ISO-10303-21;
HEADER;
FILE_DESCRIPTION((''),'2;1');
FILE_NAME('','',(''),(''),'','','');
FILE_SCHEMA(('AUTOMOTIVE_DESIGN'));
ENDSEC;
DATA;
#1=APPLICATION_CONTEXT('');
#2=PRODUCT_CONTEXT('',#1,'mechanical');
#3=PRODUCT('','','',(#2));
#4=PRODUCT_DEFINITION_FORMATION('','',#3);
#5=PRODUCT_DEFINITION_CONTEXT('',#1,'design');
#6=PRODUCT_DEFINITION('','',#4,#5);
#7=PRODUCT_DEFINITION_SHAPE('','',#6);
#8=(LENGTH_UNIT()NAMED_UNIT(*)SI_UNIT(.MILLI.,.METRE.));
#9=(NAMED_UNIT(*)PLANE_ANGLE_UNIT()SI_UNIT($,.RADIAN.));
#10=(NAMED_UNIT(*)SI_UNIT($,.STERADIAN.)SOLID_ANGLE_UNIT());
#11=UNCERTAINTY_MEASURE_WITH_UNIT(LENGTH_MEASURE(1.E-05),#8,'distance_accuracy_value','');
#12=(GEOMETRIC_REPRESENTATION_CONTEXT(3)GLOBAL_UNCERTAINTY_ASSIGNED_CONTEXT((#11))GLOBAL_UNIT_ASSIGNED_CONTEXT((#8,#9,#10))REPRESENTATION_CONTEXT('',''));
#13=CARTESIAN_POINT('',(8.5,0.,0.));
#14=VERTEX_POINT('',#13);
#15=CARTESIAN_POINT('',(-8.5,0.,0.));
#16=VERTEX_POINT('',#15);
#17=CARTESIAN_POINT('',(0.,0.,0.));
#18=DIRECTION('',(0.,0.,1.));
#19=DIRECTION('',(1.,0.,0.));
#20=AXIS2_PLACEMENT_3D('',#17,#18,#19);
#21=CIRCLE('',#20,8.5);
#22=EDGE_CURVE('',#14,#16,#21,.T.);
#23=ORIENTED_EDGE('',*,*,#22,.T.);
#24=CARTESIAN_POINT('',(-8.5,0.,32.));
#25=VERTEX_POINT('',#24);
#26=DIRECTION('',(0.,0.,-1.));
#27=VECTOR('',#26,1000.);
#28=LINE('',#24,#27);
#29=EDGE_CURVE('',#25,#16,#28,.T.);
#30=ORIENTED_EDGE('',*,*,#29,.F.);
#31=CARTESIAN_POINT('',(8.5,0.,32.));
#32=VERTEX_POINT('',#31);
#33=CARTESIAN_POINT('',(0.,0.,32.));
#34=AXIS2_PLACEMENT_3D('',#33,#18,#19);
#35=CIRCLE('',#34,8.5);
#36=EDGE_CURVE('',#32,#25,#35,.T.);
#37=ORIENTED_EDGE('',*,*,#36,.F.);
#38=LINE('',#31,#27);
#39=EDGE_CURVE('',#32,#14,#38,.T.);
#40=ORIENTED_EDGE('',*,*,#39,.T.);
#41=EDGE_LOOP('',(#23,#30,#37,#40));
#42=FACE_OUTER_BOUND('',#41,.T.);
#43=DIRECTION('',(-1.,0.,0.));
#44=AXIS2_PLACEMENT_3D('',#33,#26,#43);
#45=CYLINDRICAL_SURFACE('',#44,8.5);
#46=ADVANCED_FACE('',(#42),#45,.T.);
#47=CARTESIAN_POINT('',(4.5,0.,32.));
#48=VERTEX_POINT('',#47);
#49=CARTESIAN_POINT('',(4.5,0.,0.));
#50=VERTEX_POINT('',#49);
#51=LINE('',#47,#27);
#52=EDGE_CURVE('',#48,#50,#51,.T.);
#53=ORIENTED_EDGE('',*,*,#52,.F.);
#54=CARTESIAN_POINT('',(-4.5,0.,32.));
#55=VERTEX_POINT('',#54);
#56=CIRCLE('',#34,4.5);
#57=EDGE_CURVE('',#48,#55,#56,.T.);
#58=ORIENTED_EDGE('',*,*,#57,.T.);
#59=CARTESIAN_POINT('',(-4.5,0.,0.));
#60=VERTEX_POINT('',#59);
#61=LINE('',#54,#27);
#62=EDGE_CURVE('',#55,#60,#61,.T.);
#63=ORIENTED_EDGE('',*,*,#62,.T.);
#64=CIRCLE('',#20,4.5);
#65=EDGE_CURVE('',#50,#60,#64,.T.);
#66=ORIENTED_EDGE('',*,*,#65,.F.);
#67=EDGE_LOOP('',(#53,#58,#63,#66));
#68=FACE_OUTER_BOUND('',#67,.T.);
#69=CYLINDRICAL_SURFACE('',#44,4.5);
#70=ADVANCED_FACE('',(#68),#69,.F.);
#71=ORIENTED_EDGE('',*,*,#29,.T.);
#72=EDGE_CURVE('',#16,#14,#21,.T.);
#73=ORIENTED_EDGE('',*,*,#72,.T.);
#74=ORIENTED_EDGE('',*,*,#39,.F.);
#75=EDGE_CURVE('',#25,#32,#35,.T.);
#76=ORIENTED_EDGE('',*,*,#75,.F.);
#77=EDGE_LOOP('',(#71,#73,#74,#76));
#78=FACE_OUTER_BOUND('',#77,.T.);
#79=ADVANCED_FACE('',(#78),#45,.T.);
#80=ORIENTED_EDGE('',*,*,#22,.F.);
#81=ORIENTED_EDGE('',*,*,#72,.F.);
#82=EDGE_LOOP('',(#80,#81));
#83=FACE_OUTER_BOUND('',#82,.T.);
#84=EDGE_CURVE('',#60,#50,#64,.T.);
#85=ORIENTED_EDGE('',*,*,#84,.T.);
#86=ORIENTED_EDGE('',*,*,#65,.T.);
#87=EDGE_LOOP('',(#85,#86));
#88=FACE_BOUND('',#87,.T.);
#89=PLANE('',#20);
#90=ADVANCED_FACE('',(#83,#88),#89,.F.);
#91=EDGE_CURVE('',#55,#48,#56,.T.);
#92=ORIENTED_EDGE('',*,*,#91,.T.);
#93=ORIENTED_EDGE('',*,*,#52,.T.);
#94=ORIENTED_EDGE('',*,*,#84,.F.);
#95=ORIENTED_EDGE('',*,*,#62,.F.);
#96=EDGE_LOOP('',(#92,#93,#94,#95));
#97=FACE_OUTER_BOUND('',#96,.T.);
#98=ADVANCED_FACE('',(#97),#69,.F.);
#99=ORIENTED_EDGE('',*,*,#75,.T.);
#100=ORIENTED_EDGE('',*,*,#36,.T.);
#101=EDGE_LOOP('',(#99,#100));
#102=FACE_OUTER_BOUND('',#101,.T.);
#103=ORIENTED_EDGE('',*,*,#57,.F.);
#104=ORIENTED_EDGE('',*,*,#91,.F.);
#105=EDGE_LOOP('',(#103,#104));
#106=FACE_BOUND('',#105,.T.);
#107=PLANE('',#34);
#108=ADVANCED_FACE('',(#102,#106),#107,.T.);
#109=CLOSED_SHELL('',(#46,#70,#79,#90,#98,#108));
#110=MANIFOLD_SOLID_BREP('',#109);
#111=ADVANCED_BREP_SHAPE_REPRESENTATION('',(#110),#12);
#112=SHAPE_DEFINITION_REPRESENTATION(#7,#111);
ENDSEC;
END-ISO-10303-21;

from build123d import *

# Parameters (mm, degrees)
SKETCH1_R           = 8.5
SKETCH1_R_2         = 4.5
BOSS_EXTRUDE1_DEPTH = 32


with BuildPart() as part:
    # Sketch1 → Boss-Extrude1 (new body)
    with BuildSketch(Plane.XY):
        Circle(SKETCH1_R)
        Circle(SKETCH1_R_2, mode=Mode.SUBTRACT)
    extrude(amount=BOSS_EXTRUDE1_DEPTH)


solid = part.part
